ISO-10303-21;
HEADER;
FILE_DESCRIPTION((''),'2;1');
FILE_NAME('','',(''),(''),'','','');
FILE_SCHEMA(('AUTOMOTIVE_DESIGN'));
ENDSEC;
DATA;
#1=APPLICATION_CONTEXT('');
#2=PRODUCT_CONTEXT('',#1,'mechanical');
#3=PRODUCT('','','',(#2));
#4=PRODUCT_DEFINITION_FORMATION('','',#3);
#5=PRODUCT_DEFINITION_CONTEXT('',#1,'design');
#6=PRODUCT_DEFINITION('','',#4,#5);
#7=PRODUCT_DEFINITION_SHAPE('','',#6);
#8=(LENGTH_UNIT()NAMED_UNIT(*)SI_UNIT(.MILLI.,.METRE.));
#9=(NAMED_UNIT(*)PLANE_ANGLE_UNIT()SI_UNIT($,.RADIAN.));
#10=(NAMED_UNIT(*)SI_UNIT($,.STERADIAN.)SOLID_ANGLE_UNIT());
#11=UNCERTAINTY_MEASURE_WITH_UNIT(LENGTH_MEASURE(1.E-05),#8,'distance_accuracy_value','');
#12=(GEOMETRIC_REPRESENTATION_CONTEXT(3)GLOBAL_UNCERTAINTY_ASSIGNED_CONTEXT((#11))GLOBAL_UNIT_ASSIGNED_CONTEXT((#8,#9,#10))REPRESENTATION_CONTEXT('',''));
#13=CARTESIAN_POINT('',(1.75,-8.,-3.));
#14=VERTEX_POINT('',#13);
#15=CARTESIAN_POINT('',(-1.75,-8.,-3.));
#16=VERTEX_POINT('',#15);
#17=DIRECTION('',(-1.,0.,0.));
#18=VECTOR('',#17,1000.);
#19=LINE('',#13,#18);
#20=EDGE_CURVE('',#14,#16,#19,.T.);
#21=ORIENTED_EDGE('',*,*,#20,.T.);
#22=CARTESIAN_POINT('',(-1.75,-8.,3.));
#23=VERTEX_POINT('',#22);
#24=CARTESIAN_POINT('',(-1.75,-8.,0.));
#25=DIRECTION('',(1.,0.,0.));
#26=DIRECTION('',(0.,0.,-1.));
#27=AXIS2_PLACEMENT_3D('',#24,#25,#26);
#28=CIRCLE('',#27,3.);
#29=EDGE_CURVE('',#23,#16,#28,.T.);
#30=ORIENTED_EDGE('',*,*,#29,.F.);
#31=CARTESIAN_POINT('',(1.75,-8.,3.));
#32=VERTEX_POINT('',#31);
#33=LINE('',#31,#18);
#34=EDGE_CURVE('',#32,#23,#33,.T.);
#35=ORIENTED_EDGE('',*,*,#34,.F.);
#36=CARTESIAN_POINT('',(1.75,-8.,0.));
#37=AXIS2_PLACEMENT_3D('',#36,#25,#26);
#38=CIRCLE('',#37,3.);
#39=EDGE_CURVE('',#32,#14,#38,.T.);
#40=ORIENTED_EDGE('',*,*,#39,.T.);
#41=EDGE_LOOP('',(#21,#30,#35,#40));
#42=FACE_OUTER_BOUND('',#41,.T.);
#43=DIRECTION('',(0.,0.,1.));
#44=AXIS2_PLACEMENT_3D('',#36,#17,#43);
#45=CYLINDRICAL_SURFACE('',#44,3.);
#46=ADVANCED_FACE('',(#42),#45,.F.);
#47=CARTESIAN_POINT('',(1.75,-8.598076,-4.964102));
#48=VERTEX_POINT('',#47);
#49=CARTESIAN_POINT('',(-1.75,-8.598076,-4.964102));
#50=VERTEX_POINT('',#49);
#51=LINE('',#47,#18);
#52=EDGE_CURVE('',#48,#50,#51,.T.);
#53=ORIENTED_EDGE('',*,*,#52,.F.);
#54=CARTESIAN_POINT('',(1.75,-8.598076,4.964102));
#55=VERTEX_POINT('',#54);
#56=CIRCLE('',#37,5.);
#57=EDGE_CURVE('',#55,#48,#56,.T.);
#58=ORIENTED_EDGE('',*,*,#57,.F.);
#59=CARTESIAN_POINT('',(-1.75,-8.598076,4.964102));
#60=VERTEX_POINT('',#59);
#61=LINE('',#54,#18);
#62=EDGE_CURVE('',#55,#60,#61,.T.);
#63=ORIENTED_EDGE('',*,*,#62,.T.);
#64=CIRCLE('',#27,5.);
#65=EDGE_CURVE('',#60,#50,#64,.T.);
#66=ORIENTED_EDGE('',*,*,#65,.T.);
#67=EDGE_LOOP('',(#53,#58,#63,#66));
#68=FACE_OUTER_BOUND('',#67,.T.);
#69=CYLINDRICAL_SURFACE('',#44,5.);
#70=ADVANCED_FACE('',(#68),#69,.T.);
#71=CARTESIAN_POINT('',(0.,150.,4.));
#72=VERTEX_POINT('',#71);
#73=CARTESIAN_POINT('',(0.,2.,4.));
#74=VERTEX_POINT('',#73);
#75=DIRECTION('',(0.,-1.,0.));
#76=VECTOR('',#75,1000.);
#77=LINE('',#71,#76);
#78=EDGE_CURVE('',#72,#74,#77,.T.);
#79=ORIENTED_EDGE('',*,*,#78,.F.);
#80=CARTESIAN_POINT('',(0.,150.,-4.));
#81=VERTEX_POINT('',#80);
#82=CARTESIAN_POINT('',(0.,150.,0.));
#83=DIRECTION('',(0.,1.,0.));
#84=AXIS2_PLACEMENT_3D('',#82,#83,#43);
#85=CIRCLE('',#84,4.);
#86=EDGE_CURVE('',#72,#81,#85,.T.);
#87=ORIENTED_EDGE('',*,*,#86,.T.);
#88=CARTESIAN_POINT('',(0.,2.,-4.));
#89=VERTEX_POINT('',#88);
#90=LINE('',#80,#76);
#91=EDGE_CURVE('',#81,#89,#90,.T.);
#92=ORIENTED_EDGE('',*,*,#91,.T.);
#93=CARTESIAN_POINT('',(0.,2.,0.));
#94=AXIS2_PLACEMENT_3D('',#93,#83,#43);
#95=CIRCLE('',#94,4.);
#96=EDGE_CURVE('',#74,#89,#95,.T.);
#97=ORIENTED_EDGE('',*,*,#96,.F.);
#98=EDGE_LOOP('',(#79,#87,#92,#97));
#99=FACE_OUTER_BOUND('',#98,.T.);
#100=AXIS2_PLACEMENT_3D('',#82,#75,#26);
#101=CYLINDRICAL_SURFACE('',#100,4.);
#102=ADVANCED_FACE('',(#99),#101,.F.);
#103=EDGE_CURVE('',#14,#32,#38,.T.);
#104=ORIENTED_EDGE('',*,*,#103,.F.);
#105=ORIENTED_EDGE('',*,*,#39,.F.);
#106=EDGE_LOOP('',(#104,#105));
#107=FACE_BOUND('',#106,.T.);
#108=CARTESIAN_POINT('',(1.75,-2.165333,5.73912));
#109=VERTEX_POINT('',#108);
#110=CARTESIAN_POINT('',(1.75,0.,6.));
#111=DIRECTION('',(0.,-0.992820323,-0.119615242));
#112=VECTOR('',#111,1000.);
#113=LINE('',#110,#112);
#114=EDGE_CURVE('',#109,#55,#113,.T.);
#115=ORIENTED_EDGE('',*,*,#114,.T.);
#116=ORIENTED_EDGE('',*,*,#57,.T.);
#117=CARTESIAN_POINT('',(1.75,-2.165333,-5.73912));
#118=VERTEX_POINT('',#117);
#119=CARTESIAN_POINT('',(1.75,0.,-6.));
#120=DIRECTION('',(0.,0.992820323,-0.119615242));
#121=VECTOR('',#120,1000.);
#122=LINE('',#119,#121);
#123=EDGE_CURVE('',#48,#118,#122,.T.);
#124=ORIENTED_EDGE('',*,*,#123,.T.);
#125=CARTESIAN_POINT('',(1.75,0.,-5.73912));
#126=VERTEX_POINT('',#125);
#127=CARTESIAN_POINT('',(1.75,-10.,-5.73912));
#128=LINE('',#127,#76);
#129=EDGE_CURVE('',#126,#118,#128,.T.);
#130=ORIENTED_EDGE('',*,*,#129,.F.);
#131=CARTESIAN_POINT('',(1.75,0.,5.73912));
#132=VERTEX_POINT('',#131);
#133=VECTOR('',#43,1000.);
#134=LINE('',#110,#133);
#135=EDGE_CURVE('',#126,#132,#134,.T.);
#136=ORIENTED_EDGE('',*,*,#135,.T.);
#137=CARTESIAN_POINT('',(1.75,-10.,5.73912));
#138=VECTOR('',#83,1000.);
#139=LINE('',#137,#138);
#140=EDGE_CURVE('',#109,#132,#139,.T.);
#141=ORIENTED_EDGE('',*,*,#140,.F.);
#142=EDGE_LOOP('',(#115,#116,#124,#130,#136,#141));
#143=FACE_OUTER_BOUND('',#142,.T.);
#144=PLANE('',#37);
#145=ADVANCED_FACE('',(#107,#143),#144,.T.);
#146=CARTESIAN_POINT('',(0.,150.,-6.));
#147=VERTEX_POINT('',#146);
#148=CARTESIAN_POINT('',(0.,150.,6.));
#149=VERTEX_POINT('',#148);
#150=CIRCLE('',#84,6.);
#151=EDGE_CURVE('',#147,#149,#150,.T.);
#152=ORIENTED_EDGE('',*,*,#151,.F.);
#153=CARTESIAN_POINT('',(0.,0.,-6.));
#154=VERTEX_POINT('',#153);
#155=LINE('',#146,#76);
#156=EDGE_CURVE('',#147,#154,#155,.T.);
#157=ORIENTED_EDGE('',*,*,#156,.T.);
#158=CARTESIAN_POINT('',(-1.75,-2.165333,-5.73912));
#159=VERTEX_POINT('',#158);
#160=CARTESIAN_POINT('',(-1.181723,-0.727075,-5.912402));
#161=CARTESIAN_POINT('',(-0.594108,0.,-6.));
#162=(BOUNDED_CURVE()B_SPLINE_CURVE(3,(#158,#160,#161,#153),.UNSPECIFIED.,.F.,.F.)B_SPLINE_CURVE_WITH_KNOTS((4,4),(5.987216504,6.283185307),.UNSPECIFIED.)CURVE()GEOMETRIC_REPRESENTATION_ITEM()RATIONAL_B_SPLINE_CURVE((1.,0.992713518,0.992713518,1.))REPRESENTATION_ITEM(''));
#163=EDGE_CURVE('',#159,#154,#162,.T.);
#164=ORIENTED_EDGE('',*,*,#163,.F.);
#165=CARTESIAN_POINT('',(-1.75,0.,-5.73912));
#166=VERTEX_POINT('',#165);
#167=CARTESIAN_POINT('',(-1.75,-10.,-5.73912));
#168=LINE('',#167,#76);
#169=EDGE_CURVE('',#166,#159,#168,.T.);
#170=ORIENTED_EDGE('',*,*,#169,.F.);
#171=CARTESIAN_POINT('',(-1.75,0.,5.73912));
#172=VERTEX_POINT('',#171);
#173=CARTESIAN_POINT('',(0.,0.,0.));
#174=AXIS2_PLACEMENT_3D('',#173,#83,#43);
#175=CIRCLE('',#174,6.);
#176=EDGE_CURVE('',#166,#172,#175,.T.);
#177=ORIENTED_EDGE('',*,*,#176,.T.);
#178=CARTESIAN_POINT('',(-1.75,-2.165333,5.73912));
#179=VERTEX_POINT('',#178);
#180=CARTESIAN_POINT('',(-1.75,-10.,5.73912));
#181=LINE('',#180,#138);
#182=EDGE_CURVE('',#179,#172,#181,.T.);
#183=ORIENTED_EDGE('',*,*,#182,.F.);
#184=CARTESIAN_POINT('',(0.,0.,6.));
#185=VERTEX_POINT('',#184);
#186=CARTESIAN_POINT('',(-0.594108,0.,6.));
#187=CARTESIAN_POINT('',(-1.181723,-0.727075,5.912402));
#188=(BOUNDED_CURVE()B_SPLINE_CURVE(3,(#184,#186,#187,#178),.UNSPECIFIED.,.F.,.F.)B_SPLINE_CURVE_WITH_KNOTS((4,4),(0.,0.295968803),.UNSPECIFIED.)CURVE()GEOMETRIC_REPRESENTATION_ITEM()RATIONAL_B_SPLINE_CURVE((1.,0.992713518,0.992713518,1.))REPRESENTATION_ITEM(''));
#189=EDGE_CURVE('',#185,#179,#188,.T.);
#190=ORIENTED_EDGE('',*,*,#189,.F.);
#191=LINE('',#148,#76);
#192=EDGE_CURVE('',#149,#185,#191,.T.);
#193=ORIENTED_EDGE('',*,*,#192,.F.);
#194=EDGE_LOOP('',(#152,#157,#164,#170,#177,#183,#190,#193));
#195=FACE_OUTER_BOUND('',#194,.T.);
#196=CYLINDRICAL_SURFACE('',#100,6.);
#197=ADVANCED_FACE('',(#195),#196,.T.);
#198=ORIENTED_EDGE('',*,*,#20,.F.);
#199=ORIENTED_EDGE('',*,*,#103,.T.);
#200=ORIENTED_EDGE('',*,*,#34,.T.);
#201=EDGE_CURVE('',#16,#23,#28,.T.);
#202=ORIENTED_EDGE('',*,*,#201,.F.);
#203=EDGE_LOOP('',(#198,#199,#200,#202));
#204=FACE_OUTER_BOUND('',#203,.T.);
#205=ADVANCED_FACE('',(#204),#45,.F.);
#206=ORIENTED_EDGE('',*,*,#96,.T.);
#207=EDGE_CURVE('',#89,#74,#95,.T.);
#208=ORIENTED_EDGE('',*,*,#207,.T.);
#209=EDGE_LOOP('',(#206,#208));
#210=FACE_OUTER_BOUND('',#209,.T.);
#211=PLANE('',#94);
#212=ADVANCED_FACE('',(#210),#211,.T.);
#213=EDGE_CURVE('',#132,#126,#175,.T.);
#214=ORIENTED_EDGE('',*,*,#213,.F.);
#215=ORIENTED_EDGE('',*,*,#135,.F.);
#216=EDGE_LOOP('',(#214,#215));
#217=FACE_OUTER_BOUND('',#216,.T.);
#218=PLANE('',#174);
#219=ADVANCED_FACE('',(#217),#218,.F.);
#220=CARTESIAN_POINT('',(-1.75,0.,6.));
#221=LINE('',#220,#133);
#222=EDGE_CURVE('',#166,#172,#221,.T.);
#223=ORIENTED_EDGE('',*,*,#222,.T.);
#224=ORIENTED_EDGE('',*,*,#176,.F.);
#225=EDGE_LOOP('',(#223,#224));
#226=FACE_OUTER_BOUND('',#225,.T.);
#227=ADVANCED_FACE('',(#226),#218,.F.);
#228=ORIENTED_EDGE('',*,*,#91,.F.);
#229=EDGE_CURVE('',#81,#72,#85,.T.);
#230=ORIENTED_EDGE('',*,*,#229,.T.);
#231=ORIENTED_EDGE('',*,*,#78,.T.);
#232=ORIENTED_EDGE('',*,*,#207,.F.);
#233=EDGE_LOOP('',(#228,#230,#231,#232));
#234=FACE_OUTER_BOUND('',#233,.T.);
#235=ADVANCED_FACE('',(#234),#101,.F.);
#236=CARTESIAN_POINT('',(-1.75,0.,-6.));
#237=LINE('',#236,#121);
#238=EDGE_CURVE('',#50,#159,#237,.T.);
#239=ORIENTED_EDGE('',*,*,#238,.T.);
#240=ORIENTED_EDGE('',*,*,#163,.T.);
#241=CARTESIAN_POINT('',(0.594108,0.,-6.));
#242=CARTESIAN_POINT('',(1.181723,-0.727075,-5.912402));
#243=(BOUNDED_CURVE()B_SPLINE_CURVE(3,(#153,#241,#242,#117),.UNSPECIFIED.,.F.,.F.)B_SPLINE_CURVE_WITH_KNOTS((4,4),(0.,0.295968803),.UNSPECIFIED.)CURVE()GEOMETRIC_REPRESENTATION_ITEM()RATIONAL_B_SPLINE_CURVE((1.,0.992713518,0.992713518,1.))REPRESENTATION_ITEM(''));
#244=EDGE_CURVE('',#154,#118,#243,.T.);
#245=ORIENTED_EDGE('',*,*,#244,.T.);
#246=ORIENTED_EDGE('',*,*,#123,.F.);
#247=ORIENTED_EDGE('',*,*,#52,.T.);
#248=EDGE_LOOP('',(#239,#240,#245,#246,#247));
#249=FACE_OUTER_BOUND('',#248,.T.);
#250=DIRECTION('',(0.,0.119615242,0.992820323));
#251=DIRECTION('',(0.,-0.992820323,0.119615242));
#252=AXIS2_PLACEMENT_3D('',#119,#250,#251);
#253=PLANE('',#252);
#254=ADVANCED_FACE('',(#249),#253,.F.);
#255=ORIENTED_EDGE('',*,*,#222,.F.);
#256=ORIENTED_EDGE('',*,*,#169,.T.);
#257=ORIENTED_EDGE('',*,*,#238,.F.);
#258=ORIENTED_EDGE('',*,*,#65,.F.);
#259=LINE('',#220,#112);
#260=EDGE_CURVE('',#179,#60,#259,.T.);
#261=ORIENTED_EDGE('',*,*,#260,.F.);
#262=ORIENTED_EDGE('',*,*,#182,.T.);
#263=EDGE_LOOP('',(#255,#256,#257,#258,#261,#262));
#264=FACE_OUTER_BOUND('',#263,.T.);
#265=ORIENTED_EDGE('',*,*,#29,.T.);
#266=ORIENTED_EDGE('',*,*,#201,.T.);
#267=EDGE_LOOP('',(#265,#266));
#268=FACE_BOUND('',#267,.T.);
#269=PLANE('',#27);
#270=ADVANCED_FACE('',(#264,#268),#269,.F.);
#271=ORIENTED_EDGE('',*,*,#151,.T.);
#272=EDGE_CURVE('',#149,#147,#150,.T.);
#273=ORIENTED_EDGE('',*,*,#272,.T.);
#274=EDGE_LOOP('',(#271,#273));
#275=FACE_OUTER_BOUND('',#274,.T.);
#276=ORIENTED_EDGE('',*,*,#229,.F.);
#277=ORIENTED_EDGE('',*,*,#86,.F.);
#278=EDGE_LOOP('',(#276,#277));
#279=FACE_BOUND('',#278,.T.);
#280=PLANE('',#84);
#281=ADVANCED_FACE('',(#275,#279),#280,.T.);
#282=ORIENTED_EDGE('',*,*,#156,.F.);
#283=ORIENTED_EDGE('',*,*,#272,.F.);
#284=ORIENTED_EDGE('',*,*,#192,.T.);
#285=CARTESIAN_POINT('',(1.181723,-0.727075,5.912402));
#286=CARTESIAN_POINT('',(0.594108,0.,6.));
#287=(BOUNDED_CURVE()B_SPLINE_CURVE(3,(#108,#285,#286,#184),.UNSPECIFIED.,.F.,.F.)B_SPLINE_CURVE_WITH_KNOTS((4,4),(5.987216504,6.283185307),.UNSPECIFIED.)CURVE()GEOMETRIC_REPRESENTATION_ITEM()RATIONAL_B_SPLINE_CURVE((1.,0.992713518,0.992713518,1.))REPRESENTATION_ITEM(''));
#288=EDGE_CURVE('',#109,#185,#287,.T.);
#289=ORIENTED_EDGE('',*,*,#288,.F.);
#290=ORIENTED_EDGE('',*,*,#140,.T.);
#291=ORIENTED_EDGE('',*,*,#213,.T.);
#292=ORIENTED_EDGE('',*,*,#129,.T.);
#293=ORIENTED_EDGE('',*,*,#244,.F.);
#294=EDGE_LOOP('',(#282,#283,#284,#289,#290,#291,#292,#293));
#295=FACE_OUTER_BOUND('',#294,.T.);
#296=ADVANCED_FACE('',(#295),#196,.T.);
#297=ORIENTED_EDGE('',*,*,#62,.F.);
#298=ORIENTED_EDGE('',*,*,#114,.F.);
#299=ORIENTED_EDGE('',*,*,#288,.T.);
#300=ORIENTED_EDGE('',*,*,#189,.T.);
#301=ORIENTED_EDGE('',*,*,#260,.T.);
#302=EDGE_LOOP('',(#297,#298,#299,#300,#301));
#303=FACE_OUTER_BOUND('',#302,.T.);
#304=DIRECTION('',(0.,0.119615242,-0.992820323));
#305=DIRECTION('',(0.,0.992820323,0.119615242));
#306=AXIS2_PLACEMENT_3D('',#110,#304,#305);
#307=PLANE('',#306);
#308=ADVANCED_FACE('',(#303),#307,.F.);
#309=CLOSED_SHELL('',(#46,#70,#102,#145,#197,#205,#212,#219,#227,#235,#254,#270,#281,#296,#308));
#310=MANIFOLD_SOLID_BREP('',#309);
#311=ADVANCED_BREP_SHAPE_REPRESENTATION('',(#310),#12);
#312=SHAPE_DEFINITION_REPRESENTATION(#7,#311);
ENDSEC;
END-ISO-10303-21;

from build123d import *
from build123d.topology import SkipClean

# Parameters (mm, degrees)
SKETCH1_R           = 6
BOSS_EXTRUDE1_DEPTH = 150
SHELL1_T            = -2
SKETCH2_R           = 3
BOSS_EXTRUDE2_DEPTH = 1.75
CUT_EXTRUDE1_START  = 10
SKETCH3_R           = 8.578209266
SKETCH3_R_2         = 6
CUT_EXTRUDE1_DEPTH  = 10


with BuildPart() as part:
    # Sketch1 → Boss-Extrude1 (new body)
    with BuildSketch(Plane(origin=(0, 0, 0), x_dir=(1, 0, 0), z_dir=(0, 1, 0))):
        with Locations(Location((0, 0, 0), (0, 0, 270))):
            Circle(SKETCH1_R)
    extrude(amount=BOSS_EXTRUDE1_DEPTH)

    # Shell1
    shell1_openings = [part.faces().sort_by_distance(p)[0] for p in [
        (0, 150, 0),
    ]]
    offset(amount=SHELL1_T, openings=shell1_openings, kind=Kind.INTERSECTION)

    # Sketch2 → Boss-Extrude2 (add, symmetric)
    with BuildSketch(Plane(origin=(0, 0, 0), x_dir=(0, 0, -1), z_dir=(1, 0, 0))):
        with BuildLine():
            Line((-6, 0), (6, 0))
            Line((6, 0), (4.964101615, -8.598076211))
            ThreePointArc((4.964101615, -8.598076211), (0, -13), (-4.964101615, -8.598076211))
            Line((-4.964101615, -8.598076211), (-6, 0))
        make_face()
        with Locations((0, -8)):
            Circle(SKETCH2_R, mode=Mode.SUBTRACT)
    extrude(amount=BOSS_EXTRUDE2_DEPTH, both=True)

    # Sketch3 → Cut-Extrude1 (cut)
    with SkipClean():  # the faces are left unmerged after this step: merging them gives an invalid solid
        with BuildSketch(Plane.XZ.offset(CUT_EXTRUDE1_START)):
            Circle(SKETCH3_R)
            with Locations(Location((0, 0, 0), (0, 0, 253.0422367))):
                Circle(SKETCH3_R_2, mode=Mode.SUBTRACT)
        extrude(amount=-CUT_EXTRUDE1_DEPTH, mode=Mode.SUBTRACT)


solid = part.part
